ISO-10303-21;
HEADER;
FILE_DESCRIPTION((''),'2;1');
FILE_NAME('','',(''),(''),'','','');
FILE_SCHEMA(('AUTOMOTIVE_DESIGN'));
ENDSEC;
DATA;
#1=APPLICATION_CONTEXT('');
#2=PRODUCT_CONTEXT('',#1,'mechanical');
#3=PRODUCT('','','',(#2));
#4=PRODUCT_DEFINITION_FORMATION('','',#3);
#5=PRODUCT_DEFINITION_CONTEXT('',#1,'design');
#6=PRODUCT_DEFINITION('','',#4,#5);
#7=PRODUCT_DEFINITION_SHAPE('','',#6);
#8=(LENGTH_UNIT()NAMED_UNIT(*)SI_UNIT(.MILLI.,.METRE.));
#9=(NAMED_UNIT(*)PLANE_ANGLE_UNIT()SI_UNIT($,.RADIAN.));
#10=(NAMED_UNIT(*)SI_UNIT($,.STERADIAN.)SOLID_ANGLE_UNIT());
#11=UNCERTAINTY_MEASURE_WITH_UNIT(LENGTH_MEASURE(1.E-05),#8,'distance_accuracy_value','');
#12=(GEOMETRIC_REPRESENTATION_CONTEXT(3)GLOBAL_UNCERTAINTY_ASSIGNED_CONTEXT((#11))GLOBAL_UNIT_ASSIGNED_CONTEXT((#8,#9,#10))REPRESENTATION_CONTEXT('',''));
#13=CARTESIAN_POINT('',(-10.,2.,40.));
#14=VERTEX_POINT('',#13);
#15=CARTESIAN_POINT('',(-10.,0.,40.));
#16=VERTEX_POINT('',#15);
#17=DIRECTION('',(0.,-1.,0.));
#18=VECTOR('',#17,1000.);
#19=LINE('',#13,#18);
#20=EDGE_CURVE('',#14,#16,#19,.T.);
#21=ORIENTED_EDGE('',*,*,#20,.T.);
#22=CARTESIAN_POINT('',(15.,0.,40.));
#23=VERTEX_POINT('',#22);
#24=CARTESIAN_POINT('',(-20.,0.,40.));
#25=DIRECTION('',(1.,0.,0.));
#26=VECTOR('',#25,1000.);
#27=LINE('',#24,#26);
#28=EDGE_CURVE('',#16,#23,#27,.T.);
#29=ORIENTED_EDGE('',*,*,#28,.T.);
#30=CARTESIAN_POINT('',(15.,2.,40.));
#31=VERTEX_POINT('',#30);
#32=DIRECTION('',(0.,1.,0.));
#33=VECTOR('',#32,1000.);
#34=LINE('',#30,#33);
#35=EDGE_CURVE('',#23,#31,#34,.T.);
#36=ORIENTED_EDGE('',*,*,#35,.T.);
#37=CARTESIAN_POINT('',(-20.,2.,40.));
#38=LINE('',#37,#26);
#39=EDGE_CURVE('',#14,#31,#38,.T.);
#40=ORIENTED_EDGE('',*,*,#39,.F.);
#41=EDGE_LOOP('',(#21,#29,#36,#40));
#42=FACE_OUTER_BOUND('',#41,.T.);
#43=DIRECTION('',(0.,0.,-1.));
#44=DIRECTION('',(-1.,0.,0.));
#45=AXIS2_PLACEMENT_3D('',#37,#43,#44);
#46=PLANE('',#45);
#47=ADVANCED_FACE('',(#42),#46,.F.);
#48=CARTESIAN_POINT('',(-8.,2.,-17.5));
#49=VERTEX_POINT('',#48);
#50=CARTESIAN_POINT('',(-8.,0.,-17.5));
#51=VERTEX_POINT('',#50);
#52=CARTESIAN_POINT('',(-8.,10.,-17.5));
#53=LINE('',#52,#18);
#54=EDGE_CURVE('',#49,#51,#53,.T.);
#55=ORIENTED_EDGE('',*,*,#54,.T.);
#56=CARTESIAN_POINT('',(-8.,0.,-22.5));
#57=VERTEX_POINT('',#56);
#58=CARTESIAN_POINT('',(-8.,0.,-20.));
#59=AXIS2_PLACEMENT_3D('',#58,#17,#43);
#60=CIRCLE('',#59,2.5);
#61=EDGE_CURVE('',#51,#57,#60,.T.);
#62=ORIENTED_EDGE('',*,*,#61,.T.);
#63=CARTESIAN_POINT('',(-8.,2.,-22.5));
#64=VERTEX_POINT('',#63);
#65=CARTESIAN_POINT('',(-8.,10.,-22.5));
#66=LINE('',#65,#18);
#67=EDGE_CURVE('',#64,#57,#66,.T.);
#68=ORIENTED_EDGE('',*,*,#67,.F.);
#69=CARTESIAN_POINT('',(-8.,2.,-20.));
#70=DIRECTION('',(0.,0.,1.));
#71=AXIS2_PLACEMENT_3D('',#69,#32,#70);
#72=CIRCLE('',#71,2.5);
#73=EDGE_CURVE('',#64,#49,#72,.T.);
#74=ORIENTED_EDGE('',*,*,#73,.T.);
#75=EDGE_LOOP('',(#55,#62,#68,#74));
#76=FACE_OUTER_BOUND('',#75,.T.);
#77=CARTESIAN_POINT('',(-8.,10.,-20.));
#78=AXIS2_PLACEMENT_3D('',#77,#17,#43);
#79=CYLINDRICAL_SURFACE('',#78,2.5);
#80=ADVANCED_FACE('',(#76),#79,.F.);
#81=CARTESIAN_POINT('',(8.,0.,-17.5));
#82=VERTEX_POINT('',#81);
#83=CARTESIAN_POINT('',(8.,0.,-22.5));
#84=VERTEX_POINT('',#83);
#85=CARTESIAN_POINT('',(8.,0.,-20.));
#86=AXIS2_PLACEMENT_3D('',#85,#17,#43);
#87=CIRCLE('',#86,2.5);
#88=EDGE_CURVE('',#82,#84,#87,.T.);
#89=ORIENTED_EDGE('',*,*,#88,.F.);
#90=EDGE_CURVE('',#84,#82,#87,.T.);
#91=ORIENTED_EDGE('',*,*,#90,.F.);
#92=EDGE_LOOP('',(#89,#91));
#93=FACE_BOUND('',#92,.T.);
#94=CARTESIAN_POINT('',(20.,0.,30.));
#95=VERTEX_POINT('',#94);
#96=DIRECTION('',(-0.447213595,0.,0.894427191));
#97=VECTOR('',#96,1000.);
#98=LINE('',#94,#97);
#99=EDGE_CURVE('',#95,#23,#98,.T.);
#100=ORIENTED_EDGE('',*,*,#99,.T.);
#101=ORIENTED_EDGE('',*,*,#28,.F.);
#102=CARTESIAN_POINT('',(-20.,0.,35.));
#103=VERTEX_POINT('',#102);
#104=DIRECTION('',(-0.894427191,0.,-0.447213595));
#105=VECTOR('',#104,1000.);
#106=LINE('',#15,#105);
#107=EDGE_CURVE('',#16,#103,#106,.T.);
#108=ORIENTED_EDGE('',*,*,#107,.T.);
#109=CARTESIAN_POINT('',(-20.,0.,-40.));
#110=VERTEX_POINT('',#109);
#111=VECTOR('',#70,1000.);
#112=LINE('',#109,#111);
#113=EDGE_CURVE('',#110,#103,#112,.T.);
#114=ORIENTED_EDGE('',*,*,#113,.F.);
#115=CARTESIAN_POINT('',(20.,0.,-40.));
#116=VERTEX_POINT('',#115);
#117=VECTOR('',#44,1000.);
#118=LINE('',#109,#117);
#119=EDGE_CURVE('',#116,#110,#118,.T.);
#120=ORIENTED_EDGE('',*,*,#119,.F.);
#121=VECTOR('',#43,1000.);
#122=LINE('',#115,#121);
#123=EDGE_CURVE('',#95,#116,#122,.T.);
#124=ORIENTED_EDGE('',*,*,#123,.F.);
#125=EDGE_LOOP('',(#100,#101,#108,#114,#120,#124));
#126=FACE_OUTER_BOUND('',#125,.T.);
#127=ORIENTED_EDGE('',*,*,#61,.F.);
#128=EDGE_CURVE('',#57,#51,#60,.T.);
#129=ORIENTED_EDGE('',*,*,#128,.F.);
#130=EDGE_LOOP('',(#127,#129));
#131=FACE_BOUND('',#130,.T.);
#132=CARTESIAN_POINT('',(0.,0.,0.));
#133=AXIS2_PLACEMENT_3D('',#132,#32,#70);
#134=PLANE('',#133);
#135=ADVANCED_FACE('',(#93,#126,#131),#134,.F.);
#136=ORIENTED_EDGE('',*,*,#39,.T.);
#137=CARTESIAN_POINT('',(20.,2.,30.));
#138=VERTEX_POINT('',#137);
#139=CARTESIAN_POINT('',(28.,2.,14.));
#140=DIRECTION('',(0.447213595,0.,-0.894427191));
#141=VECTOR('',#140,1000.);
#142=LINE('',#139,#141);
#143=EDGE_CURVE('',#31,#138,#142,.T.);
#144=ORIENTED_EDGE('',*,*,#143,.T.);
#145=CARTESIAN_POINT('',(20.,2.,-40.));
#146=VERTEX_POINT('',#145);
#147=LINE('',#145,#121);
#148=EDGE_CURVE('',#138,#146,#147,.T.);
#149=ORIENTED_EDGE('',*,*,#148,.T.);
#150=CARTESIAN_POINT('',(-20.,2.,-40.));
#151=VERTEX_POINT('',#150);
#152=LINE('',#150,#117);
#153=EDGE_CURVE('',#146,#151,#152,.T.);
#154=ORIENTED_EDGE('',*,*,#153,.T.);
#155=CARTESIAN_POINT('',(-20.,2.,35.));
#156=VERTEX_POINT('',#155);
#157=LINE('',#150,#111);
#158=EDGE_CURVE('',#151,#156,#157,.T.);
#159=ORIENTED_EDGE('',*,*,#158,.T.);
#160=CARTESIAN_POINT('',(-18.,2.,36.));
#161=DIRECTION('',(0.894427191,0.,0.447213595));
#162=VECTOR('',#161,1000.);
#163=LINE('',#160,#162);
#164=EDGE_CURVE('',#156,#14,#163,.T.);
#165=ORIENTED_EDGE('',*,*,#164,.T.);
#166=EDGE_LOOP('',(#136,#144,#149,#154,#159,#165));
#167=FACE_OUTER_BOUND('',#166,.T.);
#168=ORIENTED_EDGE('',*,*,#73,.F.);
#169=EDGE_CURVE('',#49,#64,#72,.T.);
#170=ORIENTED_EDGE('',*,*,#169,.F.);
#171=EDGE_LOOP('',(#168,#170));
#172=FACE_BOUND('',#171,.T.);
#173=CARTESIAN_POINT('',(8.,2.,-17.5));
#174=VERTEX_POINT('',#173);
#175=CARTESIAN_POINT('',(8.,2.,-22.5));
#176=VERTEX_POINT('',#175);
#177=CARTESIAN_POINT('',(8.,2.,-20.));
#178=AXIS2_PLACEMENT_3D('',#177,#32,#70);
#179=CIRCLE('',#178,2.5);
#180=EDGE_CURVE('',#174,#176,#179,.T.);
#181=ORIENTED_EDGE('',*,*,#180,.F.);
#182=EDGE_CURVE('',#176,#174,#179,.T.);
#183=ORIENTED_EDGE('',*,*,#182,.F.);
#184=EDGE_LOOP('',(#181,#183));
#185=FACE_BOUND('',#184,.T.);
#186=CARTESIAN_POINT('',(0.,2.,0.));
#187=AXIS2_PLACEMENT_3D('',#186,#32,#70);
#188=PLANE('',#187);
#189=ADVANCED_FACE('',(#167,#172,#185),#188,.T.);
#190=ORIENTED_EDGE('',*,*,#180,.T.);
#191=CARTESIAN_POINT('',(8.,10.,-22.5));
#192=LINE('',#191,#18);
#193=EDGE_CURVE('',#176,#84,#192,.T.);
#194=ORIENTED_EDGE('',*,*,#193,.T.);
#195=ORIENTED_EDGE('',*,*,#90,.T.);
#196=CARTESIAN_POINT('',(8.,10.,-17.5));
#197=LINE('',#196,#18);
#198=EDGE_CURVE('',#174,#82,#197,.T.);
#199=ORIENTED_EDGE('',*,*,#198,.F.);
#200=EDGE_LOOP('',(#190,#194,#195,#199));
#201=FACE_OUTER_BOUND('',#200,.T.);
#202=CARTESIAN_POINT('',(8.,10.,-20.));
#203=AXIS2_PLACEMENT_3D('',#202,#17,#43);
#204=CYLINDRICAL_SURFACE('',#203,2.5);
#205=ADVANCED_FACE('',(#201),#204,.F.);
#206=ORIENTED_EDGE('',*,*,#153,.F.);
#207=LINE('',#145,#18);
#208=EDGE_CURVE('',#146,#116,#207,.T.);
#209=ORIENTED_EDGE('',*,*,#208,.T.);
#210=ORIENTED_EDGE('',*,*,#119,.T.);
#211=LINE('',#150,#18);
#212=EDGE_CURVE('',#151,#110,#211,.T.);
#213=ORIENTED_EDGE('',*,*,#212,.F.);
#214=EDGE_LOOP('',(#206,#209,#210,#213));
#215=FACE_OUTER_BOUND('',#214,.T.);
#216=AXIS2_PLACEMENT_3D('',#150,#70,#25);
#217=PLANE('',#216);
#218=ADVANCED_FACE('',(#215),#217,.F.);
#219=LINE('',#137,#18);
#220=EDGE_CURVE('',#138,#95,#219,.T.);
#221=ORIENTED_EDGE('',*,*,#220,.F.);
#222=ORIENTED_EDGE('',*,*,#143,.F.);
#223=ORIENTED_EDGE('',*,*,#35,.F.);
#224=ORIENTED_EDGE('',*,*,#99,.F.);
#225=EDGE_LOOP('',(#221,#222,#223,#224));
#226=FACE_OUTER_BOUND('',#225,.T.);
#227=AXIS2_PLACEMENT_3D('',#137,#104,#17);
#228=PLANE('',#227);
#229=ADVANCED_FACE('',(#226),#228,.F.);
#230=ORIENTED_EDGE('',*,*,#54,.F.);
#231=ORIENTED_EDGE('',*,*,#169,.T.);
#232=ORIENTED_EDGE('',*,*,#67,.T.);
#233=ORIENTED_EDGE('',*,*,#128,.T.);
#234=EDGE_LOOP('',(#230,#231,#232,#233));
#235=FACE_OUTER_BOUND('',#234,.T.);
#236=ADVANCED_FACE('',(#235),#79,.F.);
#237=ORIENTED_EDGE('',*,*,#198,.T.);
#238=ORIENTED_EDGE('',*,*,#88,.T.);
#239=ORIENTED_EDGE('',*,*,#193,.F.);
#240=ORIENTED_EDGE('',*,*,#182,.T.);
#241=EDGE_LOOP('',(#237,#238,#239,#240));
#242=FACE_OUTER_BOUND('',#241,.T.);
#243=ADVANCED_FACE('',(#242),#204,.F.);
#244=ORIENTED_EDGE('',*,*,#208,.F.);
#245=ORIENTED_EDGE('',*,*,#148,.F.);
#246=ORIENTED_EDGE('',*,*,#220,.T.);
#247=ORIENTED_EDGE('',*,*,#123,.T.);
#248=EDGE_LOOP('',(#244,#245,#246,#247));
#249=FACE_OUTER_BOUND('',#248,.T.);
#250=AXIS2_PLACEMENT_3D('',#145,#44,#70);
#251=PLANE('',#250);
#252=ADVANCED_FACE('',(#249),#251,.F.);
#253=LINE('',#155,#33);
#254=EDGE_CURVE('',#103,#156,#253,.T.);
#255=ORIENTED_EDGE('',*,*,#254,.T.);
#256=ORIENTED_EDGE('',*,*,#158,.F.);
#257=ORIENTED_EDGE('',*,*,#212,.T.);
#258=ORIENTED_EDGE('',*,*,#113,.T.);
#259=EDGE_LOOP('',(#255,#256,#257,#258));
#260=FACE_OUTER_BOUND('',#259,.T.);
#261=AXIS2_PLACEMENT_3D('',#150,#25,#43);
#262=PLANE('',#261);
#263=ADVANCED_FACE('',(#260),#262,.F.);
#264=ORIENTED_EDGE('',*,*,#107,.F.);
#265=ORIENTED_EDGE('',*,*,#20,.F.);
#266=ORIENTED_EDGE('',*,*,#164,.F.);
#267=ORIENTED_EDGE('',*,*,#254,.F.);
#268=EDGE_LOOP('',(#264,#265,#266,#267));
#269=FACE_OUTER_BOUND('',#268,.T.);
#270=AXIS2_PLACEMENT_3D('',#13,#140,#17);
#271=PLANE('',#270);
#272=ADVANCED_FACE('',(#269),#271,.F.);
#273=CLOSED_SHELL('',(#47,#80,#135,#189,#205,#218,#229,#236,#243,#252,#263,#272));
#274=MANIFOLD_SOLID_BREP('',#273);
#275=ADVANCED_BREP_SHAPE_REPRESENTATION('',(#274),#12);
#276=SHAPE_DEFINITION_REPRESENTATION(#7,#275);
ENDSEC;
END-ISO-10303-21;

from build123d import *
from OCP.BRepFilletAPI import BRepFilletAPI_MakeChamfer

# Parameters (mm, degrees)
SKETCH1_W           = 40
SKETCH1_H           = 80
BOSS_EXTRUDE1_DEPTH = 2
SKETCH2_R           = 2.5
CUT_EXTRUDE1_DEPTH  = 10
CHAMFER1_SIZE       = 5
CHAMFER1_SIZE2      = 10


with BuildPart() as part:
    # Sketch1 → Boss-Extrude1 (new body)
    with BuildSketch(Plane(origin=(0, 0, 0), x_dir=(1, 0, 0), z_dir=(0, 1, 0))):
        Rectangle(SKETCH1_W, SKETCH1_H)
    extrude(amount=BOSS_EXTRUDE1_DEPTH)

    # Sketch2 → Cut-Extrude1 (cut)
    with BuildSketch(Plane.XZ):
        with Locations(Location((8, -20, 0), (0, 0, 270))):
            Circle(SKETCH2_R)
        with Locations(Location((-8, -20, 0), (0, 0, 270))):
            Circle(SKETCH2_R)
    extrude(amount=-CUT_EXTRUDE1_DEPTH, mode=Mode.SUBTRACT)

    # Chamfer1: one chamfer whose edges measure the first distance from different faces: ONE call of the kernel's chamfer builder (chamfer() names one face for all edges)
    chamfer1_edges_1 = [part.edges().sort_by_distance(p)[0] for p in [
        (20, 1, 40),
    ]]
    chamfer1_side_1 = [part.faces().sort_by_distance(p)[0] for p in [
        (0, 1, 40),
    ]]
    chamfer1_edges_2 = [part.edges().sort_by_distance(p)[0] for p in [
        (-20, 1, 40),
    ]]
    chamfer1_side_2 = [part.faces().sort_by_distance(p)[0] for p in [
        (-20, 1, 0),
    ]]
    chamfer1 = BRepFilletAPI_MakeChamfer(part.part.solid().wrapped)
    for e in chamfer1_edges_1:
        chamfer1.Add(CHAMFER1_SIZE, CHAMFER1_SIZE2, e.wrapped, chamfer1_side_1[0].wrapped)  # the first distance lies on this face
    for e in chamfer1_edges_2:
        chamfer1.Add(CHAMFER1_SIZE, CHAMFER1_SIZE2, e.wrapped, chamfer1_side_2[0].wrapped)  # the first distance lies on this face
    add(Compound.cast(chamfer1.Shape()), mode=Mode.REPLACE)


solid = part.part
